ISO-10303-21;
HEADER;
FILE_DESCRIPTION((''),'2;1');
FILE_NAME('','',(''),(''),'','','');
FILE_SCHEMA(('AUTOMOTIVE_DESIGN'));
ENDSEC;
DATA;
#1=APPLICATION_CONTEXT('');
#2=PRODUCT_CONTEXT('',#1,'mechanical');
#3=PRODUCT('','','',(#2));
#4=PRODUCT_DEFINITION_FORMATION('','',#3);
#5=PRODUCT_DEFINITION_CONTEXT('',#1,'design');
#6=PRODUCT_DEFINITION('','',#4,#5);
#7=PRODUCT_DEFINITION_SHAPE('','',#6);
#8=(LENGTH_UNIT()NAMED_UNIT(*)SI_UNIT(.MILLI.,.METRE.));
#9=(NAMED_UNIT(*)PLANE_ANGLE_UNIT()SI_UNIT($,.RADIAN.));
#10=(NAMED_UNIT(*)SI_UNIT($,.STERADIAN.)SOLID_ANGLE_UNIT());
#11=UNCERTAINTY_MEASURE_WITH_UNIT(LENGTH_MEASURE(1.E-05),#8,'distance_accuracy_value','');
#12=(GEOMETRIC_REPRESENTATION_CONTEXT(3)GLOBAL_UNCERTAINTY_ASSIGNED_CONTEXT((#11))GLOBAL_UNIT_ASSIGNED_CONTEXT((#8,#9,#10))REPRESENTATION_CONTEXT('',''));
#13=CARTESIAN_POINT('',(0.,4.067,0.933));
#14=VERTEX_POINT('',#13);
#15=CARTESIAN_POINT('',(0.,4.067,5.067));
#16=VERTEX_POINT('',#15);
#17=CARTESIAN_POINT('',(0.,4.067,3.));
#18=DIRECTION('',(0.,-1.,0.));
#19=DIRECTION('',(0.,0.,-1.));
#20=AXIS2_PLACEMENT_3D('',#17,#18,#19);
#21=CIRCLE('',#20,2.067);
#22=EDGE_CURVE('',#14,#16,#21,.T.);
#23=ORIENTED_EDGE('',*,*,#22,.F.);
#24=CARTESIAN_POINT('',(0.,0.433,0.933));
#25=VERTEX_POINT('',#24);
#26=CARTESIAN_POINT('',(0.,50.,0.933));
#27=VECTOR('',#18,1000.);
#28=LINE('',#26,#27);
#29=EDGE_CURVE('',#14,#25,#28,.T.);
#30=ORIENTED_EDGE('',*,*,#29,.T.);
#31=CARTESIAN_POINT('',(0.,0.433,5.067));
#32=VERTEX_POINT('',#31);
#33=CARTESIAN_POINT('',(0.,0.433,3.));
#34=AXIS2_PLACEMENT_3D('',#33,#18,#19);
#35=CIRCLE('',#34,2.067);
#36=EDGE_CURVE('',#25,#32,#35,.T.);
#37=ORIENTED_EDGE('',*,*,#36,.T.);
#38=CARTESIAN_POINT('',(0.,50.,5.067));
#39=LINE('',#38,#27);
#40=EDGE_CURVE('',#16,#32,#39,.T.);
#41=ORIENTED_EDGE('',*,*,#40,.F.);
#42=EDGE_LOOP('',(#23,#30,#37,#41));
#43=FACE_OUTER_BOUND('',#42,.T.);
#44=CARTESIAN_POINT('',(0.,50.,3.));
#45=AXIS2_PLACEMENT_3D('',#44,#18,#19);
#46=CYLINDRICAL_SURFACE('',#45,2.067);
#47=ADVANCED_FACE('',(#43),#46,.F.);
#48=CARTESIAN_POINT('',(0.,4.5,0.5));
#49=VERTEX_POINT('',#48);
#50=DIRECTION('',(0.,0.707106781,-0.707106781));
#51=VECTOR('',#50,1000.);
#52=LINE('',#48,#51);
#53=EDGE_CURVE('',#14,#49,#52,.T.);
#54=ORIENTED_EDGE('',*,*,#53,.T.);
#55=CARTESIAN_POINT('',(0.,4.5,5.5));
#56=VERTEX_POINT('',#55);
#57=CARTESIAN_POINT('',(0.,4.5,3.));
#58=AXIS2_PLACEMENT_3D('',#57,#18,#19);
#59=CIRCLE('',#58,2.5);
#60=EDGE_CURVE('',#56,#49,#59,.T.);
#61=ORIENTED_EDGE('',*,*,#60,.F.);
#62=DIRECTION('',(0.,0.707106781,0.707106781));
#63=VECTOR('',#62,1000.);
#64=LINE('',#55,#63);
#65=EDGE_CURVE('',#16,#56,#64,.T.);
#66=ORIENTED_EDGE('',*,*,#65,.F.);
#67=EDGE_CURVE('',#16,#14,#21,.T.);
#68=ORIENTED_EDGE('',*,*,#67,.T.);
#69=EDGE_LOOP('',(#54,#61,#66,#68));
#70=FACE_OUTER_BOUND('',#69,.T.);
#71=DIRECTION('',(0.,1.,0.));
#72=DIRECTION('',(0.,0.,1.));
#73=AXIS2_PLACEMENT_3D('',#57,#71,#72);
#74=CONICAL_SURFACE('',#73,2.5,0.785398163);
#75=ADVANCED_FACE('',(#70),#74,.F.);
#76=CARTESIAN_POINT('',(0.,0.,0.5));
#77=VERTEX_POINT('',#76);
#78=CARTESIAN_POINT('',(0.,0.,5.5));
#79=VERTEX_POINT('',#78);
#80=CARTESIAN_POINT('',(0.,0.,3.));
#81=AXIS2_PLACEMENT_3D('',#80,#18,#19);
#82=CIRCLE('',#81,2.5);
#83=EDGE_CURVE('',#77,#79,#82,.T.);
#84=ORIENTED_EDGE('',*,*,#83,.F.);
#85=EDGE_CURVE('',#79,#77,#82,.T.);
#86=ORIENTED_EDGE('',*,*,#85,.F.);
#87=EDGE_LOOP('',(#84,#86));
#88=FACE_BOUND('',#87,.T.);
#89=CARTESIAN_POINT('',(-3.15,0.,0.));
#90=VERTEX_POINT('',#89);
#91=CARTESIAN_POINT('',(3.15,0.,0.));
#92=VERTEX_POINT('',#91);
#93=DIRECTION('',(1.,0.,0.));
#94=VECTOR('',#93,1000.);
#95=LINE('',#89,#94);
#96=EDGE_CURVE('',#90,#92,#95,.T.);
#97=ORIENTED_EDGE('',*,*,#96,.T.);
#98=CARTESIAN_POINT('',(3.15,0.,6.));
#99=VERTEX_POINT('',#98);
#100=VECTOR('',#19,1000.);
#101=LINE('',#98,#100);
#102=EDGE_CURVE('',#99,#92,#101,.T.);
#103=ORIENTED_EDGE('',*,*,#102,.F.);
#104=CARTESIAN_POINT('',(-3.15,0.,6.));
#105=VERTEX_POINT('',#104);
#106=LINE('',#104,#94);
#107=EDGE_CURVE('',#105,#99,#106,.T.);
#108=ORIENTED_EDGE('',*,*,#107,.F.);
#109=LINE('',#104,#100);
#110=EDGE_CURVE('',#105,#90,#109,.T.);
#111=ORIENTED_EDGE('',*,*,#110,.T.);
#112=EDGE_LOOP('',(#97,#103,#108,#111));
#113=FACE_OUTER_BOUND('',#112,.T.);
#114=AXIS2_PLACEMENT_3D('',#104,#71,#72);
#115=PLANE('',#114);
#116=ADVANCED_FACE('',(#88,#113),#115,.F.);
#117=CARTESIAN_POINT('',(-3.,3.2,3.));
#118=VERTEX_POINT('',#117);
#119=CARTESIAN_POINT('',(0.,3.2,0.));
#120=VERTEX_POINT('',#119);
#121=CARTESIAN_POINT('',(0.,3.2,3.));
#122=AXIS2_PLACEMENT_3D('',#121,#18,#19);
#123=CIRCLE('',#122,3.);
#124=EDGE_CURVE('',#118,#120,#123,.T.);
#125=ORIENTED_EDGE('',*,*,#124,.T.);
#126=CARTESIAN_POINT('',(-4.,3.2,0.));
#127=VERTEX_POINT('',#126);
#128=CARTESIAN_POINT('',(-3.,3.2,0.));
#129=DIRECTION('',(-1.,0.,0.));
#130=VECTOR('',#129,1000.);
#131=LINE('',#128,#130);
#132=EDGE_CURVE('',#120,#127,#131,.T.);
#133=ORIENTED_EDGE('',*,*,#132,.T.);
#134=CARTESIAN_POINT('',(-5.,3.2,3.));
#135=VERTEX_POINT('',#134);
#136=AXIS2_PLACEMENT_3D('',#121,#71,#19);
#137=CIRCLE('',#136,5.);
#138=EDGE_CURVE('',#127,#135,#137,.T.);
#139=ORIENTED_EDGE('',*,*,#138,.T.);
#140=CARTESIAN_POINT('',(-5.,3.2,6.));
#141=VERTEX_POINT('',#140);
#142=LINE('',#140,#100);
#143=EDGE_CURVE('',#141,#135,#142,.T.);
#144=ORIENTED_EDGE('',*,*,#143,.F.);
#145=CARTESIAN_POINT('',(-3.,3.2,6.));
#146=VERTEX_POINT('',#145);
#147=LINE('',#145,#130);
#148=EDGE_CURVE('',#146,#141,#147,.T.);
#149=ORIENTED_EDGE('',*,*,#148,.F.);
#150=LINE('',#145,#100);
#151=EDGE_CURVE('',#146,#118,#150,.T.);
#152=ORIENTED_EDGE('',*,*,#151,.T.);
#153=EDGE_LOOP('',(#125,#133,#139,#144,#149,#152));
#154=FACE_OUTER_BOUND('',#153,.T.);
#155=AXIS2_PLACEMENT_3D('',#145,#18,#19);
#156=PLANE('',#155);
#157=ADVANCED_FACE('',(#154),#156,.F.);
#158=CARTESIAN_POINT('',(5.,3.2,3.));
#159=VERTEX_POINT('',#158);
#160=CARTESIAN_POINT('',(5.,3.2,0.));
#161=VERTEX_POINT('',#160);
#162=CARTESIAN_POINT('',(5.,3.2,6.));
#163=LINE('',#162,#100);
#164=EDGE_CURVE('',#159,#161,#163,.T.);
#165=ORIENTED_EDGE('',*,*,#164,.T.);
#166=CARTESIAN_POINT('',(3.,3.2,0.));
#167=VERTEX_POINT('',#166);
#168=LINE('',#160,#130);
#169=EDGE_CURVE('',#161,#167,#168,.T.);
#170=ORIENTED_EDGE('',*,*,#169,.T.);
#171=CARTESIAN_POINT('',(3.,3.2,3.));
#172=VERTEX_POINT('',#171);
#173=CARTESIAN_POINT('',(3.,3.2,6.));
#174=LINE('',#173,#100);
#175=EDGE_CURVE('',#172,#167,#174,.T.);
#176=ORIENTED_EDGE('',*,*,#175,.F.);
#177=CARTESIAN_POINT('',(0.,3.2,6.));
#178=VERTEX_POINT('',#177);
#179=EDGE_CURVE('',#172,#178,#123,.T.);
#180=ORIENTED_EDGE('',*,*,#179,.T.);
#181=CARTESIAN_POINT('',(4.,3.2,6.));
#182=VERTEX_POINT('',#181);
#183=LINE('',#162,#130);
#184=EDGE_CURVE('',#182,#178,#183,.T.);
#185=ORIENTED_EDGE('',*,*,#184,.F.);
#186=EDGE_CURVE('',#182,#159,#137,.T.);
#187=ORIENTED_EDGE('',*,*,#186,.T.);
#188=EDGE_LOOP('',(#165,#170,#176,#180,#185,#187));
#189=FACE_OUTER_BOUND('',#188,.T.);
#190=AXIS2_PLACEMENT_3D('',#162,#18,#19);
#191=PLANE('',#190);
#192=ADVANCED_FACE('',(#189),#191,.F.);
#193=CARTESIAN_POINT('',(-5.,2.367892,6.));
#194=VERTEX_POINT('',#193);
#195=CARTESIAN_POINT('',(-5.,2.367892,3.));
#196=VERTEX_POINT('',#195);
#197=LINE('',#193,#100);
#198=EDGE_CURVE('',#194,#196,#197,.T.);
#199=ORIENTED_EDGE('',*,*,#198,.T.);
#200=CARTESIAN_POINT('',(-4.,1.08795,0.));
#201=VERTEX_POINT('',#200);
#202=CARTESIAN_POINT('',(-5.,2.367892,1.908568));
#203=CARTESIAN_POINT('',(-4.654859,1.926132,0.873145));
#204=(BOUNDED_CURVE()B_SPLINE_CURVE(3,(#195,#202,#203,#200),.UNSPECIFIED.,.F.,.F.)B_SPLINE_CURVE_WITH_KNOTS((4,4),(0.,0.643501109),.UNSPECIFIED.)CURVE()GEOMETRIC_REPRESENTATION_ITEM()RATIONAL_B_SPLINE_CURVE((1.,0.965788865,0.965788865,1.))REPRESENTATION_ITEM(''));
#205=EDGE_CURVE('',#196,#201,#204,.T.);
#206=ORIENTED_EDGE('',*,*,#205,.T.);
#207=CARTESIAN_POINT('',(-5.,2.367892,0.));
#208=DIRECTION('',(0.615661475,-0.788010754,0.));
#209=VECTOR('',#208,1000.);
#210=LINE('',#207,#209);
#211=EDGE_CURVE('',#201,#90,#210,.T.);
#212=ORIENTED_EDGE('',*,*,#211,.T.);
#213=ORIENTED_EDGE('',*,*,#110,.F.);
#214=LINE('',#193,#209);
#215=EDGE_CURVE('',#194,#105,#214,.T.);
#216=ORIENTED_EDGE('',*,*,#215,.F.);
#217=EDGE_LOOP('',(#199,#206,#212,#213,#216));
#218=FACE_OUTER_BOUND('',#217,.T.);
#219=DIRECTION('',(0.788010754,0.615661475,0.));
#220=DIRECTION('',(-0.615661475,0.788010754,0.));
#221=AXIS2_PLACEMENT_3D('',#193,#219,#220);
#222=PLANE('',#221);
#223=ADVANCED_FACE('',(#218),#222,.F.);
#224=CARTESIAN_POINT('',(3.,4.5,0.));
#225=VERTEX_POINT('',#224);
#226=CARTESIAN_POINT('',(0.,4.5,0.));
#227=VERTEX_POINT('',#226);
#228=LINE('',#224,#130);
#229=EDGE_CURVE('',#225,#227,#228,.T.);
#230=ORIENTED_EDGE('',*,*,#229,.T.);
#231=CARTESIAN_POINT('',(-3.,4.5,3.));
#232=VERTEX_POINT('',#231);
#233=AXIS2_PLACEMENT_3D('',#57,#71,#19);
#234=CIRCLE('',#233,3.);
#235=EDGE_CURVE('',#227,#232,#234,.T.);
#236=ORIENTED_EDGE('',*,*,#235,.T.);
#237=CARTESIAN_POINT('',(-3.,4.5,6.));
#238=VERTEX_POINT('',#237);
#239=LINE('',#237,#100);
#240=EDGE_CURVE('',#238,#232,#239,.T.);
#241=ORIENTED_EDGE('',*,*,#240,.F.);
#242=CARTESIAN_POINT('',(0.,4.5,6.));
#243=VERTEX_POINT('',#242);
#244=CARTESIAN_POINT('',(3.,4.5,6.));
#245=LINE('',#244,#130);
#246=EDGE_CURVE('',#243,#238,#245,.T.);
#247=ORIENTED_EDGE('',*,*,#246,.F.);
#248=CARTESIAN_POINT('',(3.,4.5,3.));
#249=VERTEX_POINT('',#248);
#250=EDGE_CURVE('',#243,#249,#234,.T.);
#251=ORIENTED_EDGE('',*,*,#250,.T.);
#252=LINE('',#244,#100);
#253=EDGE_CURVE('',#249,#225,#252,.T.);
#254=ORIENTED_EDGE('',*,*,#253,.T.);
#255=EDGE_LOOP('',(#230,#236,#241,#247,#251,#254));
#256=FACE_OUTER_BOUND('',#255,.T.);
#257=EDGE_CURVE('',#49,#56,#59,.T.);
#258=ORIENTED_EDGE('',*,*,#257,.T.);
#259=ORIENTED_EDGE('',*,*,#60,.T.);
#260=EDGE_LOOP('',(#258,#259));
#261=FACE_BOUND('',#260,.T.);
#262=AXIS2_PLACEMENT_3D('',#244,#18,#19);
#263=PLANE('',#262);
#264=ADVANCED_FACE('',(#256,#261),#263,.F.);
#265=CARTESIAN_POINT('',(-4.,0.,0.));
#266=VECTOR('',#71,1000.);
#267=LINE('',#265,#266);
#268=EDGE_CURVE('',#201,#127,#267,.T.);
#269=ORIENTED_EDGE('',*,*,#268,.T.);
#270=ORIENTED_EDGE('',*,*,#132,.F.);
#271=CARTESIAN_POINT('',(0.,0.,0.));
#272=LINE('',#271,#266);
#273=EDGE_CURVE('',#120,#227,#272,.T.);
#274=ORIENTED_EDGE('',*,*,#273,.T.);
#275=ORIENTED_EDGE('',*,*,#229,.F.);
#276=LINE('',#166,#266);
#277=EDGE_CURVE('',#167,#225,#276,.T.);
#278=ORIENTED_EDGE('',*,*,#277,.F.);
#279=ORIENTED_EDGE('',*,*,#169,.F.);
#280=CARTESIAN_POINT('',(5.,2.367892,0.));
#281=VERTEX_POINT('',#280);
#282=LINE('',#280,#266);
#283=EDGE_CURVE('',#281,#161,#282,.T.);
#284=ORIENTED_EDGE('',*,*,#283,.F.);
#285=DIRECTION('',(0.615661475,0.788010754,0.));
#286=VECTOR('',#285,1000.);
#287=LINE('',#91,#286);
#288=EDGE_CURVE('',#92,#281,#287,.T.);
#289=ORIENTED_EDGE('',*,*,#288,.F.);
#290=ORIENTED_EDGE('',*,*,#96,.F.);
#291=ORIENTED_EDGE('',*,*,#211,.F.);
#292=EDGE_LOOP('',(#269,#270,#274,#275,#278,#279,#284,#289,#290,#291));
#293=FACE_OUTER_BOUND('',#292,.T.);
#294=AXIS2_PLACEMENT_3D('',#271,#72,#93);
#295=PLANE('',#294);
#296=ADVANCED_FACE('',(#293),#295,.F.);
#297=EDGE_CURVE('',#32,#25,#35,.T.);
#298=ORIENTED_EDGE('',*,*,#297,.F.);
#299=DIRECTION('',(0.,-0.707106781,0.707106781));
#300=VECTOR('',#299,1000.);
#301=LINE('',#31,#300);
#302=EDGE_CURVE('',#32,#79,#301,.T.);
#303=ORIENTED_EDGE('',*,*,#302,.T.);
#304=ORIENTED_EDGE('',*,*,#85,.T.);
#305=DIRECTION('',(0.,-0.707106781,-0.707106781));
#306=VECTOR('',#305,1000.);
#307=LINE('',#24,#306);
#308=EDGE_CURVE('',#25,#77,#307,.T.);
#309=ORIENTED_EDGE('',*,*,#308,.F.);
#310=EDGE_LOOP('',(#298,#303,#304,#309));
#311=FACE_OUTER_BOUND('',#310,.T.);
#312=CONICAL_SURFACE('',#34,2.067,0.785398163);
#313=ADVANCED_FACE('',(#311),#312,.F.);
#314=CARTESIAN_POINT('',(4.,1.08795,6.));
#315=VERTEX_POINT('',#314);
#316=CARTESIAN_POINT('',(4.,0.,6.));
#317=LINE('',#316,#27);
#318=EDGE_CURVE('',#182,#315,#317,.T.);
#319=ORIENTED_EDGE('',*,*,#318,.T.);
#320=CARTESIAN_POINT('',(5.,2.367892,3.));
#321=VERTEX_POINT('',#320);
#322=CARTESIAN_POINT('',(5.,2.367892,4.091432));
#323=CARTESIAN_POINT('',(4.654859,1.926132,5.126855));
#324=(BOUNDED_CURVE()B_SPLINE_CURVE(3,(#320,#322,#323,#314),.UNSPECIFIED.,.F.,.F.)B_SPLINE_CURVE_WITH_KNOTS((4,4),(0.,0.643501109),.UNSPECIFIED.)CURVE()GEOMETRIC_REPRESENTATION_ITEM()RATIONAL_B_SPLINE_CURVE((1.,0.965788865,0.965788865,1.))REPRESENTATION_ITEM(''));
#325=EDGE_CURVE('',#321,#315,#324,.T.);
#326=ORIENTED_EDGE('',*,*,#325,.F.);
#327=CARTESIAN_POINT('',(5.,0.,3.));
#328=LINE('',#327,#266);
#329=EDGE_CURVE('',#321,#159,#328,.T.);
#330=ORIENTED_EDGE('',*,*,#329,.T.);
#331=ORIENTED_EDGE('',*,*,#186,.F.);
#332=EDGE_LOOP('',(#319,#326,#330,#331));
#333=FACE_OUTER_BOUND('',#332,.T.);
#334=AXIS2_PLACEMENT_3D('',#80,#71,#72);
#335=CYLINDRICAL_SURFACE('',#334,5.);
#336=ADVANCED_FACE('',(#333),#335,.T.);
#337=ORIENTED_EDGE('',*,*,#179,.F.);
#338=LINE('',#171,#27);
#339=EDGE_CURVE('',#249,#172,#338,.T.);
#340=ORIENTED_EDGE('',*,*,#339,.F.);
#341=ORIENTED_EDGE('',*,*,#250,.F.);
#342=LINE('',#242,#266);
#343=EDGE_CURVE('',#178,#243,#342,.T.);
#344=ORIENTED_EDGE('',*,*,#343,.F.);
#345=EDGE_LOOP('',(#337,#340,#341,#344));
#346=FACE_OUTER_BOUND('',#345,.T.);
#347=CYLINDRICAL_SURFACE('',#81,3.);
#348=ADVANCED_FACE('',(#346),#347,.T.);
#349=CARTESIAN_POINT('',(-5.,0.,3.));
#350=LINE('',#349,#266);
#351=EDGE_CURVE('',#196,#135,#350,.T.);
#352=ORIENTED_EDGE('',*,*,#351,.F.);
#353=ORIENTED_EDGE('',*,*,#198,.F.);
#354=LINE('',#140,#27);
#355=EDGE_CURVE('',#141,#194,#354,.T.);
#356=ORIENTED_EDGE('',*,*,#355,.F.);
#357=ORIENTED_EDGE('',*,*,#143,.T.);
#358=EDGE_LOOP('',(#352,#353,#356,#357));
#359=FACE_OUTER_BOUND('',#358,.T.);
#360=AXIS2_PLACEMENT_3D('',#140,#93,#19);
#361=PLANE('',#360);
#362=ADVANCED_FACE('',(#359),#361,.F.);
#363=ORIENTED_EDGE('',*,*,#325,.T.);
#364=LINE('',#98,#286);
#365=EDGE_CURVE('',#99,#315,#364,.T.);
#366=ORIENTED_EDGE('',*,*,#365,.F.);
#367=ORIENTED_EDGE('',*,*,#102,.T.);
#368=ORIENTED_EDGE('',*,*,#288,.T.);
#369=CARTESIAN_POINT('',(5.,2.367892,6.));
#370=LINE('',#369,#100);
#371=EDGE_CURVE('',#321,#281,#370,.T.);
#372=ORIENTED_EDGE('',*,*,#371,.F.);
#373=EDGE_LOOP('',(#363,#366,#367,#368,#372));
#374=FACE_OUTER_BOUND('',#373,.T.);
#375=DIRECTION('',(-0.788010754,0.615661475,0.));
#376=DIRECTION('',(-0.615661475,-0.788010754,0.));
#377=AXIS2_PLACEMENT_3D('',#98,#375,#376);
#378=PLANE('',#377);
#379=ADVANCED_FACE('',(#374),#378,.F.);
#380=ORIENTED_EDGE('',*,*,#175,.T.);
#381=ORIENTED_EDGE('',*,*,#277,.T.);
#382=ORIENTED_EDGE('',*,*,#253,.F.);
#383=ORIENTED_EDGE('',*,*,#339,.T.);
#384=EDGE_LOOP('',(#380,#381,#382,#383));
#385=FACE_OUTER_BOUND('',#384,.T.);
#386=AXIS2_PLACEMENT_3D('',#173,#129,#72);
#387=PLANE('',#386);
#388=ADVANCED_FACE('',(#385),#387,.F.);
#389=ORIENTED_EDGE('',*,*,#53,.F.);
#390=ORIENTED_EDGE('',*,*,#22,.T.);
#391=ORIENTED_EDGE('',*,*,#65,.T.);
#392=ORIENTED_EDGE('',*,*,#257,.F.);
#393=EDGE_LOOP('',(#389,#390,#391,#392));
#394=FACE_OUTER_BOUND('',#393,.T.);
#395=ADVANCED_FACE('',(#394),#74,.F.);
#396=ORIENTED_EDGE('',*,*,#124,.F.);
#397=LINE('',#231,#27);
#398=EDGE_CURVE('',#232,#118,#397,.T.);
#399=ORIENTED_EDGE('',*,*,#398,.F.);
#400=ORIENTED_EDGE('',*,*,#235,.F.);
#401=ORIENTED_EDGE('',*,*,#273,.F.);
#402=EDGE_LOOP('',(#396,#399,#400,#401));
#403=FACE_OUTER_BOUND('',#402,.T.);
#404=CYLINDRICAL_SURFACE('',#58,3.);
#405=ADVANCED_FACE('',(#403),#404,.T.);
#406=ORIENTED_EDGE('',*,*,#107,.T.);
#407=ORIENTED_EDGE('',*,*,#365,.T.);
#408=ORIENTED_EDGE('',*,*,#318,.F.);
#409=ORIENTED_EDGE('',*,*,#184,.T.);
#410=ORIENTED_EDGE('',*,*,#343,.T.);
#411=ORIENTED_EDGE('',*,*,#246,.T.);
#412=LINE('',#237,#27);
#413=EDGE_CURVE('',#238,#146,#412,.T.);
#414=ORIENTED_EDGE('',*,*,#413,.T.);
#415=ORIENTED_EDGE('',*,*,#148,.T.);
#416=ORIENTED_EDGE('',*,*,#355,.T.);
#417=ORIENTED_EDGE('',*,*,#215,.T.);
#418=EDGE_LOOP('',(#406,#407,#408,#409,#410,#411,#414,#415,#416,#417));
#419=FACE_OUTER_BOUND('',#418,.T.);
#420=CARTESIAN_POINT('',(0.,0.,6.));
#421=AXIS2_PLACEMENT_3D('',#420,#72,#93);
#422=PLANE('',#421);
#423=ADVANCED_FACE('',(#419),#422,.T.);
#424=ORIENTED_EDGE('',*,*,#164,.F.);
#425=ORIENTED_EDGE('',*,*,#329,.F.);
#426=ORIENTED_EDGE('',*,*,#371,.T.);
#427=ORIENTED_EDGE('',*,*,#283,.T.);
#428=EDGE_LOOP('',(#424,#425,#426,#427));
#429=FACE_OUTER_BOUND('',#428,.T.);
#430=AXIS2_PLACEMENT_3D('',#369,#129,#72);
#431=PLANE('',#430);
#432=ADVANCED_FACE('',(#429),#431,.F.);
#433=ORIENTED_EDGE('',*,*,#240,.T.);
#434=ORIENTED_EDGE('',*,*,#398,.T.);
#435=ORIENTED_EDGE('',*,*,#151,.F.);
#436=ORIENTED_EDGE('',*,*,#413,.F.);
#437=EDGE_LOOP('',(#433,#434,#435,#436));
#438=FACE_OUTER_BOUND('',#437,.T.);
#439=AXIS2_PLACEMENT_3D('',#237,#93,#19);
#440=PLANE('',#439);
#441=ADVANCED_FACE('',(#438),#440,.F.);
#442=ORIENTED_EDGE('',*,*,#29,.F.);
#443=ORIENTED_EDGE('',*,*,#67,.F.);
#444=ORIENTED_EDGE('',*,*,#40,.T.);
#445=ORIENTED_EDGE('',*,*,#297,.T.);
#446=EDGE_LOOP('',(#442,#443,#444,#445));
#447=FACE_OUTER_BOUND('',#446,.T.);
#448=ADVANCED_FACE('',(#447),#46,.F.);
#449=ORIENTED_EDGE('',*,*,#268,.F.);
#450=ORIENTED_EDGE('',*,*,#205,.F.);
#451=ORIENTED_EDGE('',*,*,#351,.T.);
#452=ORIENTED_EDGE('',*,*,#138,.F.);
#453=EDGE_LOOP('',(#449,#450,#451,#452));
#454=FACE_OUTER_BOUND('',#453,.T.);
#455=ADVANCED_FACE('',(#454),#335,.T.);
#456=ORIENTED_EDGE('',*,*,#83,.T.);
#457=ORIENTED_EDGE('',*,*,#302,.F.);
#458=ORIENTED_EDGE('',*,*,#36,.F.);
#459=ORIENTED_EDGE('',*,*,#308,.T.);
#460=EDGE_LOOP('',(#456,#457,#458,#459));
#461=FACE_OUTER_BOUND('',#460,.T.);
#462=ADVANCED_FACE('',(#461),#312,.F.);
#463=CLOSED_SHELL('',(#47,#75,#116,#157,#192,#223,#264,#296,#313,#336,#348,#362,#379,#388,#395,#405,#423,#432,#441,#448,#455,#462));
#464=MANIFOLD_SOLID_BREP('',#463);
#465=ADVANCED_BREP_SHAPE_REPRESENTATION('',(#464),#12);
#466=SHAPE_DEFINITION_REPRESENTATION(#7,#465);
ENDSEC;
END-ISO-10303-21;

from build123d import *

# Parameters (mm, degrees)
EXTRUDE_1_DEPTH     = 6
CUT_EXTRUDE_1_DEPTH = 4.5
CUT_EXTRUDE_2_DEPTH = 4.5
FILLET_1_R          = 3


with BuildPart() as part:
    # 草图1 → 凸台-拉伸1 (new body)
    with BuildSketch(Plane.XY):
        Polygon((-5, 2.36789202), (-3.15, 0), (3.15, 0), (5, 2.36789202), (5, 3.2), (3, 3.2), (3, 4.5), (-3, 4.5), (-3, 3.2), (-5, 3.2), align=None)
    extrude(amount=EXTRUDE_1_DEPTH)

    # 草图2 → 切除-旋转1 (revolve, cut)
    with BuildSketch(Plane(origin=(0, 0, 0), x_dir=(0, 0, -1), z_dir=(1, 0, 0)), mode=Mode.PRIVATE) as cut_revolve_1_sk:
        Polygon((-3, 0), (-5.5, 0), (-5.067, 0.433), (-5.067, 4.067), (-5.5, 4.5), (-3, 4.5), align=None)
    revolve(cut_revolve_1_sk.sketch.rotate(Axis((0, 50, 3), (0, -1, 0)), 180), axis=Axis((0, 50, 3), (0, -1, 0)), mode=Mode.SUBTRACT)

    # 草图3 → 切除-拉伸1 (cut)
    with BuildSketch(Plane(origin=(0, 4.5, 0), x_dir=(1, 0, 0), z_dir=(0, 1, 0))):
        with BuildLine():
            Line((4, -6), (5, -6))
            Line((5, -6), (5, -3))
            ThreePointArc((5, -3), (4.74341649, -4.58113883), (4, -6))
        make_face()
    extrude(amount=-CUT_EXTRUDE_1_DEPTH, mode=Mode.SUBTRACT)

    # 草图4 → 切除-拉伸2 (cut)
    with BuildSketch(Plane(origin=(0, 4.5, 0), x_dir=(1, 0, 0), z_dir=(0, 1, 0))):
        with BuildLine():
            Line((-4, 0), (-5, 0))
            Line((-5, 0), (-5, -3))
            ThreePointArc((-5, -3), (-4.74341649, -1.41886117), (-4, 0))
        make_face()
    extrude(amount=-CUT_EXTRUDE_2_DEPTH, mode=Mode.SUBTRACT)

    # 圆角1
    fillet_1_edges = [part.edges().sort_by_distance(p)[0] for p in [
        (3, 3.85, 6),
        (-3, 3.85, 0),
    ]]
    fillet(fillet_1_edges, radius=FILLET_1_R)


solid = part.part
